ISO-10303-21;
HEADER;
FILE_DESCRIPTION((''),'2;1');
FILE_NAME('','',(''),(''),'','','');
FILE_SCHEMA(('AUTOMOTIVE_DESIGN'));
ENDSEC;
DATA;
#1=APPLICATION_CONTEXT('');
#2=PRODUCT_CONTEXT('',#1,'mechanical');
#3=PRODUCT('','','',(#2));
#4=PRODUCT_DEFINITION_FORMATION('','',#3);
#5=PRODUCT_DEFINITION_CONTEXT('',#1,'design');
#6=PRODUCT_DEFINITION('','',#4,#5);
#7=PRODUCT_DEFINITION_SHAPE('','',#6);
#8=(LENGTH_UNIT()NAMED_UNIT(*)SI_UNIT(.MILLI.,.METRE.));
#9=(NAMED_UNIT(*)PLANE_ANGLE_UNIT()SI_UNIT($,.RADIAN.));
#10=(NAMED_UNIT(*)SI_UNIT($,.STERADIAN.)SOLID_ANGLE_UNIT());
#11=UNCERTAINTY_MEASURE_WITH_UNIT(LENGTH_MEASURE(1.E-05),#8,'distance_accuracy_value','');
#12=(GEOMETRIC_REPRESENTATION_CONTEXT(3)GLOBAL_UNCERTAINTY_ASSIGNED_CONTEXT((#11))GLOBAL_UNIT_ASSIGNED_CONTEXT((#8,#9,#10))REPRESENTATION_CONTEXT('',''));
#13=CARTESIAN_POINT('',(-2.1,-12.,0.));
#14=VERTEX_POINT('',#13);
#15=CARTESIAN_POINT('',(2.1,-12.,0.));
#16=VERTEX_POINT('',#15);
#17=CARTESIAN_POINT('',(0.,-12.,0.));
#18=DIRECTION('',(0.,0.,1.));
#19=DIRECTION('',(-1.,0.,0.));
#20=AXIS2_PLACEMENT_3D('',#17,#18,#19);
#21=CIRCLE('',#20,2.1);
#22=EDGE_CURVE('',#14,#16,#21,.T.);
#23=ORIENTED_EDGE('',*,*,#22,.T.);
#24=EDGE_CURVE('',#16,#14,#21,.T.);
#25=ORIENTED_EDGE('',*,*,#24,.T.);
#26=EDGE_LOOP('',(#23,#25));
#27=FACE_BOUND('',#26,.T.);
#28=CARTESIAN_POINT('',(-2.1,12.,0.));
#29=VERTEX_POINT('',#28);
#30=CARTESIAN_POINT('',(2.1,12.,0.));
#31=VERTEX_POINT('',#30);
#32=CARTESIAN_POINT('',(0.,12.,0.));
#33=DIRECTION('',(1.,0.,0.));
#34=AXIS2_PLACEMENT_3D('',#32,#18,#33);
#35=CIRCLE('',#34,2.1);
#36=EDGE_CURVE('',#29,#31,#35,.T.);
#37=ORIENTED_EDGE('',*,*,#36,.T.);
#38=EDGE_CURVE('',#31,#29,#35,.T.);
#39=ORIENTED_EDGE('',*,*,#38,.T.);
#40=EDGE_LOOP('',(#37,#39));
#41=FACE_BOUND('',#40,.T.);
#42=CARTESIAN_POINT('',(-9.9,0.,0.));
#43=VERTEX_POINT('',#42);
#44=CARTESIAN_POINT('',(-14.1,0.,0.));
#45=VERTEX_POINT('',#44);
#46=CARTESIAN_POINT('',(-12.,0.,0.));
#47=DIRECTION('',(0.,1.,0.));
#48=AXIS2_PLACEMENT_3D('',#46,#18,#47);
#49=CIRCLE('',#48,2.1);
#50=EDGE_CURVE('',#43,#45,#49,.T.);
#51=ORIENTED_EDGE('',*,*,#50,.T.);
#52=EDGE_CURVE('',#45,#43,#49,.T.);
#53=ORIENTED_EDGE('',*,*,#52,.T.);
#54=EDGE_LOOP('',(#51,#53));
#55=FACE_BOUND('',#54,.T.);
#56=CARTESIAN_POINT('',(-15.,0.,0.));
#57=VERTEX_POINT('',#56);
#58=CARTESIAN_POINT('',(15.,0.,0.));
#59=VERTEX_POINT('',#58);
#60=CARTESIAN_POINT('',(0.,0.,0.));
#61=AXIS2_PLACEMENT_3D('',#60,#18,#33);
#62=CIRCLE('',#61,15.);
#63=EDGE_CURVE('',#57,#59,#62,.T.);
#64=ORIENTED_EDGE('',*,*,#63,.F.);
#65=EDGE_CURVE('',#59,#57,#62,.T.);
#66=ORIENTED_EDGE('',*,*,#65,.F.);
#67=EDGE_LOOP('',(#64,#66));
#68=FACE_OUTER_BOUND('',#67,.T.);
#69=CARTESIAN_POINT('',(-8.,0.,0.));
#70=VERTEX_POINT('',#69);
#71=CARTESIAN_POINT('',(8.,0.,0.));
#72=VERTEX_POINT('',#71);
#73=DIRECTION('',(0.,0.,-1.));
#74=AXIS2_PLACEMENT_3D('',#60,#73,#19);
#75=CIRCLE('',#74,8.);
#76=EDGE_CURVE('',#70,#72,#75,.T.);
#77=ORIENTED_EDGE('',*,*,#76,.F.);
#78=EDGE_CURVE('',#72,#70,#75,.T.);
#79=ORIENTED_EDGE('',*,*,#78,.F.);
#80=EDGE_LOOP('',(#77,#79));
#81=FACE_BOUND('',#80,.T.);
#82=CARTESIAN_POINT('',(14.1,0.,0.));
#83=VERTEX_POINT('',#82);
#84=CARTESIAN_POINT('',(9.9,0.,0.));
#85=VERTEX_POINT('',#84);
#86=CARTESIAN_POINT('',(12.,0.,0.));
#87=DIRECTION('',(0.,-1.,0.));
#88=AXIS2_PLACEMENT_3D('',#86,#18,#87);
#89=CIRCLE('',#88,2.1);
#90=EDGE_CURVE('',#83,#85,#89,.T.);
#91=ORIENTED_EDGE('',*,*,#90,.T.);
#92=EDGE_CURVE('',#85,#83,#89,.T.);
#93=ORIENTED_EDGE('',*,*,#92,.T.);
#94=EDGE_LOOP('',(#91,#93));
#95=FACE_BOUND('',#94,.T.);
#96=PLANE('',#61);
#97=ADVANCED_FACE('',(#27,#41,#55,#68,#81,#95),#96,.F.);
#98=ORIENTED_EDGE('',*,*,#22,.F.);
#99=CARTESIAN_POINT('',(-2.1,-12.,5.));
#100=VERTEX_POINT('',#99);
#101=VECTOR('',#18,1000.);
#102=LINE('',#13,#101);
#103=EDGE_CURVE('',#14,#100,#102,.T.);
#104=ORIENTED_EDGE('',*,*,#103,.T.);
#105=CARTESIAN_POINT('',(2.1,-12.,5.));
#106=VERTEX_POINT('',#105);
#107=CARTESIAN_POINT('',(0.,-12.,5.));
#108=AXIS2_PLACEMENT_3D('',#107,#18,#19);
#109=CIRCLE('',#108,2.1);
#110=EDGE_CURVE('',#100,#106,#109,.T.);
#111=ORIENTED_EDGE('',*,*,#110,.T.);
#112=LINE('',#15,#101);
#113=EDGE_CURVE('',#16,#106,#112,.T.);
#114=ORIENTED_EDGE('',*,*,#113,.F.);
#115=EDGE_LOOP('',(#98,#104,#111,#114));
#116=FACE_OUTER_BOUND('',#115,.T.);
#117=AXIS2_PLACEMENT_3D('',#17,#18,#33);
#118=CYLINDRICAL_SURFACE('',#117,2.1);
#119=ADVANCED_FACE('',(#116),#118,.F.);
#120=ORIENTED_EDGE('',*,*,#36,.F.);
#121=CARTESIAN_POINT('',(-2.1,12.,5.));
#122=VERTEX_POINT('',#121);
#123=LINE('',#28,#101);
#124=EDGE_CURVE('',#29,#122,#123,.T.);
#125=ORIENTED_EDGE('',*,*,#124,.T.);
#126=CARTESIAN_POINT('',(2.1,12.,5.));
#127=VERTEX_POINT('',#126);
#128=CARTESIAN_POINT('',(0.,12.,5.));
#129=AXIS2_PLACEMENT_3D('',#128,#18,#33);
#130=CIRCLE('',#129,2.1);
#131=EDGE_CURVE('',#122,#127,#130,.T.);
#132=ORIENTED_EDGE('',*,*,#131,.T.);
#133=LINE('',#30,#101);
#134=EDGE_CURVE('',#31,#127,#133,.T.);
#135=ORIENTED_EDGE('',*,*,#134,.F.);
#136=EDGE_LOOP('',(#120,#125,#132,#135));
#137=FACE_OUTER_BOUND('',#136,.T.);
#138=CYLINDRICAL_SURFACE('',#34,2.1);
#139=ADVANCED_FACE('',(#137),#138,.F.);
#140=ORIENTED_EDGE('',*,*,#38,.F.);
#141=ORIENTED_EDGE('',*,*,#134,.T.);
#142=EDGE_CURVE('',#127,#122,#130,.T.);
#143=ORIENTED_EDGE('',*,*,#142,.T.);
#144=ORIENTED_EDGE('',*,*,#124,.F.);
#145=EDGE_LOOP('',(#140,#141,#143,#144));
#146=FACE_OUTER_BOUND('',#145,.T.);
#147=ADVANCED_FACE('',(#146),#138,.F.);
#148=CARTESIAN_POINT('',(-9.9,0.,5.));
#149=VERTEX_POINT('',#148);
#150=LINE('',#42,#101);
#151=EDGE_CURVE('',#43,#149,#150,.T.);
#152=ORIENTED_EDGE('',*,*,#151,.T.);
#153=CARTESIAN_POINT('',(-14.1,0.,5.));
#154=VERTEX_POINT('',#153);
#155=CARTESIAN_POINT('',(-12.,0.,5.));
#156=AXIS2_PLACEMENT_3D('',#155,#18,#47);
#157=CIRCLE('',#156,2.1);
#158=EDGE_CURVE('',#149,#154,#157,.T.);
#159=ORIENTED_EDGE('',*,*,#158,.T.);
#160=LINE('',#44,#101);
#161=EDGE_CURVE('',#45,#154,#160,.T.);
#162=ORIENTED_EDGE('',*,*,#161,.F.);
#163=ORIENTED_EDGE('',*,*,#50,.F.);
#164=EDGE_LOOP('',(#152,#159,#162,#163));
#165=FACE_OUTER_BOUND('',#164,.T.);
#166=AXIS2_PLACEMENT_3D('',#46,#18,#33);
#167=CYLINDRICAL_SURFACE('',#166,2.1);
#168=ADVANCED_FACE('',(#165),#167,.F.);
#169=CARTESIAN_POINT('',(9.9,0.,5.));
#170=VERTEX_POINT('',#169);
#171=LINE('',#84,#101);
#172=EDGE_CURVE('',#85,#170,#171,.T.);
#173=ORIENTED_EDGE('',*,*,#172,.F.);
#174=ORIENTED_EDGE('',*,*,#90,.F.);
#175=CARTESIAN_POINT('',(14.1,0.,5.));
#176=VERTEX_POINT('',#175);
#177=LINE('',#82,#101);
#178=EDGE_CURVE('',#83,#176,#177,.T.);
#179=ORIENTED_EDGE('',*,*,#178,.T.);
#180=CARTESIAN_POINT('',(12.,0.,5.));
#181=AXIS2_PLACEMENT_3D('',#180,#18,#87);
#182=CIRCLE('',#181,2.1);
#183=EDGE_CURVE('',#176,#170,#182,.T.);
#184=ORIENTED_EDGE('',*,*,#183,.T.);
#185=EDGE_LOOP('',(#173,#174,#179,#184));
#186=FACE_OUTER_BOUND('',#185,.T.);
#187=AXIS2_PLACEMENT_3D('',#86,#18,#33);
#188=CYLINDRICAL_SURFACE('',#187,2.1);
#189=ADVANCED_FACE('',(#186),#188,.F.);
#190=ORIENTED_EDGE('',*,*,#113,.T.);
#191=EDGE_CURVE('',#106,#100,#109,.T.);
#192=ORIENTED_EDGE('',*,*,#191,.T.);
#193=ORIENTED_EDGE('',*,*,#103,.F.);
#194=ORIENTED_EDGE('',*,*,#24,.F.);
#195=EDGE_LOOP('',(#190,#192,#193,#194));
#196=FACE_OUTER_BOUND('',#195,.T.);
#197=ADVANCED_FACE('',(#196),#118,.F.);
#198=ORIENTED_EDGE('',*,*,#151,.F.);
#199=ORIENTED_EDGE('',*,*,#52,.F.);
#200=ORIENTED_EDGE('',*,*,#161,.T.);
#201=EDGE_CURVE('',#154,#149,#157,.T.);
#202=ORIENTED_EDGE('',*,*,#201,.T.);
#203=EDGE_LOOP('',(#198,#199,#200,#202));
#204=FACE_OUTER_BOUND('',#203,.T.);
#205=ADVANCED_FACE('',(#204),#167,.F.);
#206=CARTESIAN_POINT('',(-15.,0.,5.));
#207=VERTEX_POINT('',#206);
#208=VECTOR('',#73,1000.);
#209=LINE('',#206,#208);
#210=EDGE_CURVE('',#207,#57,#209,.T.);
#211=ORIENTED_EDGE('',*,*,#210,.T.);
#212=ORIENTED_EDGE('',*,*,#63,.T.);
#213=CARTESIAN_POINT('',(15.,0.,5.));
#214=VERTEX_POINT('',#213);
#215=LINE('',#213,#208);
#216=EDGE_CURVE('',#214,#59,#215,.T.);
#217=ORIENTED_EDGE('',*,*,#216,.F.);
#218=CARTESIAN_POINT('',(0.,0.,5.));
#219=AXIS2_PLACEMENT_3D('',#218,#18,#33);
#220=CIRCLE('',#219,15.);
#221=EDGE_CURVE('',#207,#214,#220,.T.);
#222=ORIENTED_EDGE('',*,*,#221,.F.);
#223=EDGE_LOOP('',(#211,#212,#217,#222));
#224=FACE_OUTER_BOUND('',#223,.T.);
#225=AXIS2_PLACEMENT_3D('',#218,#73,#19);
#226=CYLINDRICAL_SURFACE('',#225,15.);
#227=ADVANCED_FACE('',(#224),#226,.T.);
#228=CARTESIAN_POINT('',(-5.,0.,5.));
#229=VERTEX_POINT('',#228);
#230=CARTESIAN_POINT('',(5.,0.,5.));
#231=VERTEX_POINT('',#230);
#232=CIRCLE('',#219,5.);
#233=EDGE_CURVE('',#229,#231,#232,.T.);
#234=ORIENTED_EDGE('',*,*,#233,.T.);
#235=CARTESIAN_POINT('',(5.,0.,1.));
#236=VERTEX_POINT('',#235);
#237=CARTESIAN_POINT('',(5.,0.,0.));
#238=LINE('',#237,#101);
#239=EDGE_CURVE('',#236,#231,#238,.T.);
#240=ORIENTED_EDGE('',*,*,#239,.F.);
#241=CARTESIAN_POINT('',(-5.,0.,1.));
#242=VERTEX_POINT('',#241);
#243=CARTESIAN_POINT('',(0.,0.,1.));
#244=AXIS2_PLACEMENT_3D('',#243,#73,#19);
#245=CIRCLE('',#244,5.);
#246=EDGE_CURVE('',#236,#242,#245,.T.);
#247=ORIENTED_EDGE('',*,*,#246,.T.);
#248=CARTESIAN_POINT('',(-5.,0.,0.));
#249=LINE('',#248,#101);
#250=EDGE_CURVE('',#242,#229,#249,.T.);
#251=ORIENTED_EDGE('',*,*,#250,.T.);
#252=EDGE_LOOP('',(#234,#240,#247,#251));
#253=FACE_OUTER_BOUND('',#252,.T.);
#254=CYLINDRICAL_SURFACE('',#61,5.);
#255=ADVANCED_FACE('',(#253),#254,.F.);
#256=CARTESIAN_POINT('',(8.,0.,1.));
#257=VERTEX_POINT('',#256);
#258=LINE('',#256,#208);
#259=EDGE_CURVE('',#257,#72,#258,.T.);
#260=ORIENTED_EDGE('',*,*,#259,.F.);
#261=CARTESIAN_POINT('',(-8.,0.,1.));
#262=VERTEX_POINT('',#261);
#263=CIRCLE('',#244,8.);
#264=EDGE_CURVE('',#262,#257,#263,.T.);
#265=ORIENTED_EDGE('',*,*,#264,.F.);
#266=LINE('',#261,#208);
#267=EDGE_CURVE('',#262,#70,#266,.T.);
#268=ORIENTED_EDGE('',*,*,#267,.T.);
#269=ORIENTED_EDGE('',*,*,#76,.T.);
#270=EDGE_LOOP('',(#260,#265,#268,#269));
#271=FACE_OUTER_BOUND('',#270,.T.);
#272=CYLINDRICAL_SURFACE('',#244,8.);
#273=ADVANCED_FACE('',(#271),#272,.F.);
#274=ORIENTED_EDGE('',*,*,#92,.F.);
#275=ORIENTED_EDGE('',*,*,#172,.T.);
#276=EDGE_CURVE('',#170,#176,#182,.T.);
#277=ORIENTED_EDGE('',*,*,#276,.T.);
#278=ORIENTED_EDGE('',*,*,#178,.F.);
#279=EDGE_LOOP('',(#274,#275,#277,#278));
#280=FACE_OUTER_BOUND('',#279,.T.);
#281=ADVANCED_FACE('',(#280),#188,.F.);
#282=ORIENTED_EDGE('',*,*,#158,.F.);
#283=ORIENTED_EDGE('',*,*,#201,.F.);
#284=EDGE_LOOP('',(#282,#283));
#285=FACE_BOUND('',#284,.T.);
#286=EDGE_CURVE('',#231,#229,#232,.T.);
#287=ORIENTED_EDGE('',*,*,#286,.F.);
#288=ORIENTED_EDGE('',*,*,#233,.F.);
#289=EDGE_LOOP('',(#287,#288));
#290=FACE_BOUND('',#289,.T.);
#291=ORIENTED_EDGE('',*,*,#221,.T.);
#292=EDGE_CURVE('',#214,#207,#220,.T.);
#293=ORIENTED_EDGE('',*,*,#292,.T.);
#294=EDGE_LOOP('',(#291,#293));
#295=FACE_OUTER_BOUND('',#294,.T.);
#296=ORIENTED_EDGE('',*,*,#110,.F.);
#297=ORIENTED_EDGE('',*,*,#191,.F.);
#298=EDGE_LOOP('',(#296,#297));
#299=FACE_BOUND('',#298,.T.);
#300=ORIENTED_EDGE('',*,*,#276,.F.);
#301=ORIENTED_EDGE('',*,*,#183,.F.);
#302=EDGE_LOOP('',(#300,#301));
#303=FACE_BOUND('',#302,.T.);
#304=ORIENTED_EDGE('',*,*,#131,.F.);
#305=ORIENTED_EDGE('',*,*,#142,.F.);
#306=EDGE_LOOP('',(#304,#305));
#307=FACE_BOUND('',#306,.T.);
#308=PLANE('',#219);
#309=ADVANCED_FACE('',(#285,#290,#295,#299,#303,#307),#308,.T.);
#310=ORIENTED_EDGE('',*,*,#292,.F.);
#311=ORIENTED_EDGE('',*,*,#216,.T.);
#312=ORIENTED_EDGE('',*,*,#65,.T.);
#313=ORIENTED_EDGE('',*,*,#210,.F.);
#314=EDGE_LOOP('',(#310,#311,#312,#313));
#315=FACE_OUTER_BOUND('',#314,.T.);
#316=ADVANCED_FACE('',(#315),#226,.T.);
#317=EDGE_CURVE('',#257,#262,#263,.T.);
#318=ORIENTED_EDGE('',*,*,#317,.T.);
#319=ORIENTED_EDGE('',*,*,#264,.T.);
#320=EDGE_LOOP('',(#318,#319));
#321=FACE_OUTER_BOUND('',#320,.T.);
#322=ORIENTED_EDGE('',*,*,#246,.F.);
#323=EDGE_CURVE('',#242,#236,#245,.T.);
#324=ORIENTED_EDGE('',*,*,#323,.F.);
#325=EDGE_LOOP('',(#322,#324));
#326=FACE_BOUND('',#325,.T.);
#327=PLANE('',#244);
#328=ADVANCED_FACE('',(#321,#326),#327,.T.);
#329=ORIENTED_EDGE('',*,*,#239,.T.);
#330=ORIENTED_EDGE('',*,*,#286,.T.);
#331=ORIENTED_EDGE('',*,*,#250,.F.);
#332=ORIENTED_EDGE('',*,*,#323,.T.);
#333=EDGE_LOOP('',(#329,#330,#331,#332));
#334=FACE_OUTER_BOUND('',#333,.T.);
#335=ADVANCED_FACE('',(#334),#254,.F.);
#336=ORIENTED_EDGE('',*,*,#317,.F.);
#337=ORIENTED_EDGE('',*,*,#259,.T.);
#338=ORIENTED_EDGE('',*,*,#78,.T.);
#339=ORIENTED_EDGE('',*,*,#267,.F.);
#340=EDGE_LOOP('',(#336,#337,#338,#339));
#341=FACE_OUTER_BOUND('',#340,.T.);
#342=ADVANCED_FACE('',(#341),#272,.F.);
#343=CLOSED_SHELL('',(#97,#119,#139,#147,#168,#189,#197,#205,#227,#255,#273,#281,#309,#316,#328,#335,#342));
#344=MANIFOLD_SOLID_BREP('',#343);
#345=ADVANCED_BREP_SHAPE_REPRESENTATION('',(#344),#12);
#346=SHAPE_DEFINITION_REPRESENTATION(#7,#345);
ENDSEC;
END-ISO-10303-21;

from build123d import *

# Parameters (mm, degrees)
SKETCH1_R           = 15
BOSS_EXTRUDE1_DEPTH = 5
SKETCH2_R           = 2.1
CUT_EXTRUDE1_DEPTH  = 22.794494718
CIRPATTERN1_COUNT   = 4
SKETCH3_R           = 8
CUT_EXTRUDE2_DEPTH  = 1
SKETCH4_R           = 5
CUT_EXTRUDE3_DEPTH  = 22.794494718


with BuildPart() as part:
    # Sketch1 → Boss-Extrude1 (new body)
    with BuildSketch(Plane.XY):
        Circle(SKETCH1_R)
    extrude(amount=BOSS_EXTRUDE1_DEPTH)

    # Sketch2 → Cut-Extrude1 (cut, through all)
    with BuildSketch(Plane.XY.offset(5)):
        with Locations((0, 12)):
            Circle(SKETCH2_R)
    cut_extrude1 = extrude(amount=-CUT_EXTRUDE1_DEPTH, mode=Mode.SUBTRACT)

    # CirPattern1: Cut-Extrude1 ×4 about axis
    cirpattern1_axis = Axis((0, 0, 0), (0, 0, 1))
    for i in range(1, CIRPATTERN1_COUNT):
        add(cut_extrude1.rotate(cirpattern1_axis, i * 360 / CIRPATTERN1_COUNT), mode=Mode.SUBTRACT)

    # Sketch3 → Cut-Extrude2 (cut)
    with BuildSketch(Plane(origin=(0, 0, 0), x_dir=(-1, 0, 0), z_dir=(0, 0, -1))):
        Circle(SKETCH3_R)
    extrude(amount=-CUT_EXTRUDE2_DEPTH, mode=Mode.SUBTRACT)

    # Sketch4 → Cut-Extrude3 (cut, through all)
    with BuildSketch(Plane.XY.offset(5)):
        Circle(SKETCH4_R)
    extrude(amount=-CUT_EXTRUDE3_DEPTH, mode=Mode.SUBTRACT)


solid = part.part
